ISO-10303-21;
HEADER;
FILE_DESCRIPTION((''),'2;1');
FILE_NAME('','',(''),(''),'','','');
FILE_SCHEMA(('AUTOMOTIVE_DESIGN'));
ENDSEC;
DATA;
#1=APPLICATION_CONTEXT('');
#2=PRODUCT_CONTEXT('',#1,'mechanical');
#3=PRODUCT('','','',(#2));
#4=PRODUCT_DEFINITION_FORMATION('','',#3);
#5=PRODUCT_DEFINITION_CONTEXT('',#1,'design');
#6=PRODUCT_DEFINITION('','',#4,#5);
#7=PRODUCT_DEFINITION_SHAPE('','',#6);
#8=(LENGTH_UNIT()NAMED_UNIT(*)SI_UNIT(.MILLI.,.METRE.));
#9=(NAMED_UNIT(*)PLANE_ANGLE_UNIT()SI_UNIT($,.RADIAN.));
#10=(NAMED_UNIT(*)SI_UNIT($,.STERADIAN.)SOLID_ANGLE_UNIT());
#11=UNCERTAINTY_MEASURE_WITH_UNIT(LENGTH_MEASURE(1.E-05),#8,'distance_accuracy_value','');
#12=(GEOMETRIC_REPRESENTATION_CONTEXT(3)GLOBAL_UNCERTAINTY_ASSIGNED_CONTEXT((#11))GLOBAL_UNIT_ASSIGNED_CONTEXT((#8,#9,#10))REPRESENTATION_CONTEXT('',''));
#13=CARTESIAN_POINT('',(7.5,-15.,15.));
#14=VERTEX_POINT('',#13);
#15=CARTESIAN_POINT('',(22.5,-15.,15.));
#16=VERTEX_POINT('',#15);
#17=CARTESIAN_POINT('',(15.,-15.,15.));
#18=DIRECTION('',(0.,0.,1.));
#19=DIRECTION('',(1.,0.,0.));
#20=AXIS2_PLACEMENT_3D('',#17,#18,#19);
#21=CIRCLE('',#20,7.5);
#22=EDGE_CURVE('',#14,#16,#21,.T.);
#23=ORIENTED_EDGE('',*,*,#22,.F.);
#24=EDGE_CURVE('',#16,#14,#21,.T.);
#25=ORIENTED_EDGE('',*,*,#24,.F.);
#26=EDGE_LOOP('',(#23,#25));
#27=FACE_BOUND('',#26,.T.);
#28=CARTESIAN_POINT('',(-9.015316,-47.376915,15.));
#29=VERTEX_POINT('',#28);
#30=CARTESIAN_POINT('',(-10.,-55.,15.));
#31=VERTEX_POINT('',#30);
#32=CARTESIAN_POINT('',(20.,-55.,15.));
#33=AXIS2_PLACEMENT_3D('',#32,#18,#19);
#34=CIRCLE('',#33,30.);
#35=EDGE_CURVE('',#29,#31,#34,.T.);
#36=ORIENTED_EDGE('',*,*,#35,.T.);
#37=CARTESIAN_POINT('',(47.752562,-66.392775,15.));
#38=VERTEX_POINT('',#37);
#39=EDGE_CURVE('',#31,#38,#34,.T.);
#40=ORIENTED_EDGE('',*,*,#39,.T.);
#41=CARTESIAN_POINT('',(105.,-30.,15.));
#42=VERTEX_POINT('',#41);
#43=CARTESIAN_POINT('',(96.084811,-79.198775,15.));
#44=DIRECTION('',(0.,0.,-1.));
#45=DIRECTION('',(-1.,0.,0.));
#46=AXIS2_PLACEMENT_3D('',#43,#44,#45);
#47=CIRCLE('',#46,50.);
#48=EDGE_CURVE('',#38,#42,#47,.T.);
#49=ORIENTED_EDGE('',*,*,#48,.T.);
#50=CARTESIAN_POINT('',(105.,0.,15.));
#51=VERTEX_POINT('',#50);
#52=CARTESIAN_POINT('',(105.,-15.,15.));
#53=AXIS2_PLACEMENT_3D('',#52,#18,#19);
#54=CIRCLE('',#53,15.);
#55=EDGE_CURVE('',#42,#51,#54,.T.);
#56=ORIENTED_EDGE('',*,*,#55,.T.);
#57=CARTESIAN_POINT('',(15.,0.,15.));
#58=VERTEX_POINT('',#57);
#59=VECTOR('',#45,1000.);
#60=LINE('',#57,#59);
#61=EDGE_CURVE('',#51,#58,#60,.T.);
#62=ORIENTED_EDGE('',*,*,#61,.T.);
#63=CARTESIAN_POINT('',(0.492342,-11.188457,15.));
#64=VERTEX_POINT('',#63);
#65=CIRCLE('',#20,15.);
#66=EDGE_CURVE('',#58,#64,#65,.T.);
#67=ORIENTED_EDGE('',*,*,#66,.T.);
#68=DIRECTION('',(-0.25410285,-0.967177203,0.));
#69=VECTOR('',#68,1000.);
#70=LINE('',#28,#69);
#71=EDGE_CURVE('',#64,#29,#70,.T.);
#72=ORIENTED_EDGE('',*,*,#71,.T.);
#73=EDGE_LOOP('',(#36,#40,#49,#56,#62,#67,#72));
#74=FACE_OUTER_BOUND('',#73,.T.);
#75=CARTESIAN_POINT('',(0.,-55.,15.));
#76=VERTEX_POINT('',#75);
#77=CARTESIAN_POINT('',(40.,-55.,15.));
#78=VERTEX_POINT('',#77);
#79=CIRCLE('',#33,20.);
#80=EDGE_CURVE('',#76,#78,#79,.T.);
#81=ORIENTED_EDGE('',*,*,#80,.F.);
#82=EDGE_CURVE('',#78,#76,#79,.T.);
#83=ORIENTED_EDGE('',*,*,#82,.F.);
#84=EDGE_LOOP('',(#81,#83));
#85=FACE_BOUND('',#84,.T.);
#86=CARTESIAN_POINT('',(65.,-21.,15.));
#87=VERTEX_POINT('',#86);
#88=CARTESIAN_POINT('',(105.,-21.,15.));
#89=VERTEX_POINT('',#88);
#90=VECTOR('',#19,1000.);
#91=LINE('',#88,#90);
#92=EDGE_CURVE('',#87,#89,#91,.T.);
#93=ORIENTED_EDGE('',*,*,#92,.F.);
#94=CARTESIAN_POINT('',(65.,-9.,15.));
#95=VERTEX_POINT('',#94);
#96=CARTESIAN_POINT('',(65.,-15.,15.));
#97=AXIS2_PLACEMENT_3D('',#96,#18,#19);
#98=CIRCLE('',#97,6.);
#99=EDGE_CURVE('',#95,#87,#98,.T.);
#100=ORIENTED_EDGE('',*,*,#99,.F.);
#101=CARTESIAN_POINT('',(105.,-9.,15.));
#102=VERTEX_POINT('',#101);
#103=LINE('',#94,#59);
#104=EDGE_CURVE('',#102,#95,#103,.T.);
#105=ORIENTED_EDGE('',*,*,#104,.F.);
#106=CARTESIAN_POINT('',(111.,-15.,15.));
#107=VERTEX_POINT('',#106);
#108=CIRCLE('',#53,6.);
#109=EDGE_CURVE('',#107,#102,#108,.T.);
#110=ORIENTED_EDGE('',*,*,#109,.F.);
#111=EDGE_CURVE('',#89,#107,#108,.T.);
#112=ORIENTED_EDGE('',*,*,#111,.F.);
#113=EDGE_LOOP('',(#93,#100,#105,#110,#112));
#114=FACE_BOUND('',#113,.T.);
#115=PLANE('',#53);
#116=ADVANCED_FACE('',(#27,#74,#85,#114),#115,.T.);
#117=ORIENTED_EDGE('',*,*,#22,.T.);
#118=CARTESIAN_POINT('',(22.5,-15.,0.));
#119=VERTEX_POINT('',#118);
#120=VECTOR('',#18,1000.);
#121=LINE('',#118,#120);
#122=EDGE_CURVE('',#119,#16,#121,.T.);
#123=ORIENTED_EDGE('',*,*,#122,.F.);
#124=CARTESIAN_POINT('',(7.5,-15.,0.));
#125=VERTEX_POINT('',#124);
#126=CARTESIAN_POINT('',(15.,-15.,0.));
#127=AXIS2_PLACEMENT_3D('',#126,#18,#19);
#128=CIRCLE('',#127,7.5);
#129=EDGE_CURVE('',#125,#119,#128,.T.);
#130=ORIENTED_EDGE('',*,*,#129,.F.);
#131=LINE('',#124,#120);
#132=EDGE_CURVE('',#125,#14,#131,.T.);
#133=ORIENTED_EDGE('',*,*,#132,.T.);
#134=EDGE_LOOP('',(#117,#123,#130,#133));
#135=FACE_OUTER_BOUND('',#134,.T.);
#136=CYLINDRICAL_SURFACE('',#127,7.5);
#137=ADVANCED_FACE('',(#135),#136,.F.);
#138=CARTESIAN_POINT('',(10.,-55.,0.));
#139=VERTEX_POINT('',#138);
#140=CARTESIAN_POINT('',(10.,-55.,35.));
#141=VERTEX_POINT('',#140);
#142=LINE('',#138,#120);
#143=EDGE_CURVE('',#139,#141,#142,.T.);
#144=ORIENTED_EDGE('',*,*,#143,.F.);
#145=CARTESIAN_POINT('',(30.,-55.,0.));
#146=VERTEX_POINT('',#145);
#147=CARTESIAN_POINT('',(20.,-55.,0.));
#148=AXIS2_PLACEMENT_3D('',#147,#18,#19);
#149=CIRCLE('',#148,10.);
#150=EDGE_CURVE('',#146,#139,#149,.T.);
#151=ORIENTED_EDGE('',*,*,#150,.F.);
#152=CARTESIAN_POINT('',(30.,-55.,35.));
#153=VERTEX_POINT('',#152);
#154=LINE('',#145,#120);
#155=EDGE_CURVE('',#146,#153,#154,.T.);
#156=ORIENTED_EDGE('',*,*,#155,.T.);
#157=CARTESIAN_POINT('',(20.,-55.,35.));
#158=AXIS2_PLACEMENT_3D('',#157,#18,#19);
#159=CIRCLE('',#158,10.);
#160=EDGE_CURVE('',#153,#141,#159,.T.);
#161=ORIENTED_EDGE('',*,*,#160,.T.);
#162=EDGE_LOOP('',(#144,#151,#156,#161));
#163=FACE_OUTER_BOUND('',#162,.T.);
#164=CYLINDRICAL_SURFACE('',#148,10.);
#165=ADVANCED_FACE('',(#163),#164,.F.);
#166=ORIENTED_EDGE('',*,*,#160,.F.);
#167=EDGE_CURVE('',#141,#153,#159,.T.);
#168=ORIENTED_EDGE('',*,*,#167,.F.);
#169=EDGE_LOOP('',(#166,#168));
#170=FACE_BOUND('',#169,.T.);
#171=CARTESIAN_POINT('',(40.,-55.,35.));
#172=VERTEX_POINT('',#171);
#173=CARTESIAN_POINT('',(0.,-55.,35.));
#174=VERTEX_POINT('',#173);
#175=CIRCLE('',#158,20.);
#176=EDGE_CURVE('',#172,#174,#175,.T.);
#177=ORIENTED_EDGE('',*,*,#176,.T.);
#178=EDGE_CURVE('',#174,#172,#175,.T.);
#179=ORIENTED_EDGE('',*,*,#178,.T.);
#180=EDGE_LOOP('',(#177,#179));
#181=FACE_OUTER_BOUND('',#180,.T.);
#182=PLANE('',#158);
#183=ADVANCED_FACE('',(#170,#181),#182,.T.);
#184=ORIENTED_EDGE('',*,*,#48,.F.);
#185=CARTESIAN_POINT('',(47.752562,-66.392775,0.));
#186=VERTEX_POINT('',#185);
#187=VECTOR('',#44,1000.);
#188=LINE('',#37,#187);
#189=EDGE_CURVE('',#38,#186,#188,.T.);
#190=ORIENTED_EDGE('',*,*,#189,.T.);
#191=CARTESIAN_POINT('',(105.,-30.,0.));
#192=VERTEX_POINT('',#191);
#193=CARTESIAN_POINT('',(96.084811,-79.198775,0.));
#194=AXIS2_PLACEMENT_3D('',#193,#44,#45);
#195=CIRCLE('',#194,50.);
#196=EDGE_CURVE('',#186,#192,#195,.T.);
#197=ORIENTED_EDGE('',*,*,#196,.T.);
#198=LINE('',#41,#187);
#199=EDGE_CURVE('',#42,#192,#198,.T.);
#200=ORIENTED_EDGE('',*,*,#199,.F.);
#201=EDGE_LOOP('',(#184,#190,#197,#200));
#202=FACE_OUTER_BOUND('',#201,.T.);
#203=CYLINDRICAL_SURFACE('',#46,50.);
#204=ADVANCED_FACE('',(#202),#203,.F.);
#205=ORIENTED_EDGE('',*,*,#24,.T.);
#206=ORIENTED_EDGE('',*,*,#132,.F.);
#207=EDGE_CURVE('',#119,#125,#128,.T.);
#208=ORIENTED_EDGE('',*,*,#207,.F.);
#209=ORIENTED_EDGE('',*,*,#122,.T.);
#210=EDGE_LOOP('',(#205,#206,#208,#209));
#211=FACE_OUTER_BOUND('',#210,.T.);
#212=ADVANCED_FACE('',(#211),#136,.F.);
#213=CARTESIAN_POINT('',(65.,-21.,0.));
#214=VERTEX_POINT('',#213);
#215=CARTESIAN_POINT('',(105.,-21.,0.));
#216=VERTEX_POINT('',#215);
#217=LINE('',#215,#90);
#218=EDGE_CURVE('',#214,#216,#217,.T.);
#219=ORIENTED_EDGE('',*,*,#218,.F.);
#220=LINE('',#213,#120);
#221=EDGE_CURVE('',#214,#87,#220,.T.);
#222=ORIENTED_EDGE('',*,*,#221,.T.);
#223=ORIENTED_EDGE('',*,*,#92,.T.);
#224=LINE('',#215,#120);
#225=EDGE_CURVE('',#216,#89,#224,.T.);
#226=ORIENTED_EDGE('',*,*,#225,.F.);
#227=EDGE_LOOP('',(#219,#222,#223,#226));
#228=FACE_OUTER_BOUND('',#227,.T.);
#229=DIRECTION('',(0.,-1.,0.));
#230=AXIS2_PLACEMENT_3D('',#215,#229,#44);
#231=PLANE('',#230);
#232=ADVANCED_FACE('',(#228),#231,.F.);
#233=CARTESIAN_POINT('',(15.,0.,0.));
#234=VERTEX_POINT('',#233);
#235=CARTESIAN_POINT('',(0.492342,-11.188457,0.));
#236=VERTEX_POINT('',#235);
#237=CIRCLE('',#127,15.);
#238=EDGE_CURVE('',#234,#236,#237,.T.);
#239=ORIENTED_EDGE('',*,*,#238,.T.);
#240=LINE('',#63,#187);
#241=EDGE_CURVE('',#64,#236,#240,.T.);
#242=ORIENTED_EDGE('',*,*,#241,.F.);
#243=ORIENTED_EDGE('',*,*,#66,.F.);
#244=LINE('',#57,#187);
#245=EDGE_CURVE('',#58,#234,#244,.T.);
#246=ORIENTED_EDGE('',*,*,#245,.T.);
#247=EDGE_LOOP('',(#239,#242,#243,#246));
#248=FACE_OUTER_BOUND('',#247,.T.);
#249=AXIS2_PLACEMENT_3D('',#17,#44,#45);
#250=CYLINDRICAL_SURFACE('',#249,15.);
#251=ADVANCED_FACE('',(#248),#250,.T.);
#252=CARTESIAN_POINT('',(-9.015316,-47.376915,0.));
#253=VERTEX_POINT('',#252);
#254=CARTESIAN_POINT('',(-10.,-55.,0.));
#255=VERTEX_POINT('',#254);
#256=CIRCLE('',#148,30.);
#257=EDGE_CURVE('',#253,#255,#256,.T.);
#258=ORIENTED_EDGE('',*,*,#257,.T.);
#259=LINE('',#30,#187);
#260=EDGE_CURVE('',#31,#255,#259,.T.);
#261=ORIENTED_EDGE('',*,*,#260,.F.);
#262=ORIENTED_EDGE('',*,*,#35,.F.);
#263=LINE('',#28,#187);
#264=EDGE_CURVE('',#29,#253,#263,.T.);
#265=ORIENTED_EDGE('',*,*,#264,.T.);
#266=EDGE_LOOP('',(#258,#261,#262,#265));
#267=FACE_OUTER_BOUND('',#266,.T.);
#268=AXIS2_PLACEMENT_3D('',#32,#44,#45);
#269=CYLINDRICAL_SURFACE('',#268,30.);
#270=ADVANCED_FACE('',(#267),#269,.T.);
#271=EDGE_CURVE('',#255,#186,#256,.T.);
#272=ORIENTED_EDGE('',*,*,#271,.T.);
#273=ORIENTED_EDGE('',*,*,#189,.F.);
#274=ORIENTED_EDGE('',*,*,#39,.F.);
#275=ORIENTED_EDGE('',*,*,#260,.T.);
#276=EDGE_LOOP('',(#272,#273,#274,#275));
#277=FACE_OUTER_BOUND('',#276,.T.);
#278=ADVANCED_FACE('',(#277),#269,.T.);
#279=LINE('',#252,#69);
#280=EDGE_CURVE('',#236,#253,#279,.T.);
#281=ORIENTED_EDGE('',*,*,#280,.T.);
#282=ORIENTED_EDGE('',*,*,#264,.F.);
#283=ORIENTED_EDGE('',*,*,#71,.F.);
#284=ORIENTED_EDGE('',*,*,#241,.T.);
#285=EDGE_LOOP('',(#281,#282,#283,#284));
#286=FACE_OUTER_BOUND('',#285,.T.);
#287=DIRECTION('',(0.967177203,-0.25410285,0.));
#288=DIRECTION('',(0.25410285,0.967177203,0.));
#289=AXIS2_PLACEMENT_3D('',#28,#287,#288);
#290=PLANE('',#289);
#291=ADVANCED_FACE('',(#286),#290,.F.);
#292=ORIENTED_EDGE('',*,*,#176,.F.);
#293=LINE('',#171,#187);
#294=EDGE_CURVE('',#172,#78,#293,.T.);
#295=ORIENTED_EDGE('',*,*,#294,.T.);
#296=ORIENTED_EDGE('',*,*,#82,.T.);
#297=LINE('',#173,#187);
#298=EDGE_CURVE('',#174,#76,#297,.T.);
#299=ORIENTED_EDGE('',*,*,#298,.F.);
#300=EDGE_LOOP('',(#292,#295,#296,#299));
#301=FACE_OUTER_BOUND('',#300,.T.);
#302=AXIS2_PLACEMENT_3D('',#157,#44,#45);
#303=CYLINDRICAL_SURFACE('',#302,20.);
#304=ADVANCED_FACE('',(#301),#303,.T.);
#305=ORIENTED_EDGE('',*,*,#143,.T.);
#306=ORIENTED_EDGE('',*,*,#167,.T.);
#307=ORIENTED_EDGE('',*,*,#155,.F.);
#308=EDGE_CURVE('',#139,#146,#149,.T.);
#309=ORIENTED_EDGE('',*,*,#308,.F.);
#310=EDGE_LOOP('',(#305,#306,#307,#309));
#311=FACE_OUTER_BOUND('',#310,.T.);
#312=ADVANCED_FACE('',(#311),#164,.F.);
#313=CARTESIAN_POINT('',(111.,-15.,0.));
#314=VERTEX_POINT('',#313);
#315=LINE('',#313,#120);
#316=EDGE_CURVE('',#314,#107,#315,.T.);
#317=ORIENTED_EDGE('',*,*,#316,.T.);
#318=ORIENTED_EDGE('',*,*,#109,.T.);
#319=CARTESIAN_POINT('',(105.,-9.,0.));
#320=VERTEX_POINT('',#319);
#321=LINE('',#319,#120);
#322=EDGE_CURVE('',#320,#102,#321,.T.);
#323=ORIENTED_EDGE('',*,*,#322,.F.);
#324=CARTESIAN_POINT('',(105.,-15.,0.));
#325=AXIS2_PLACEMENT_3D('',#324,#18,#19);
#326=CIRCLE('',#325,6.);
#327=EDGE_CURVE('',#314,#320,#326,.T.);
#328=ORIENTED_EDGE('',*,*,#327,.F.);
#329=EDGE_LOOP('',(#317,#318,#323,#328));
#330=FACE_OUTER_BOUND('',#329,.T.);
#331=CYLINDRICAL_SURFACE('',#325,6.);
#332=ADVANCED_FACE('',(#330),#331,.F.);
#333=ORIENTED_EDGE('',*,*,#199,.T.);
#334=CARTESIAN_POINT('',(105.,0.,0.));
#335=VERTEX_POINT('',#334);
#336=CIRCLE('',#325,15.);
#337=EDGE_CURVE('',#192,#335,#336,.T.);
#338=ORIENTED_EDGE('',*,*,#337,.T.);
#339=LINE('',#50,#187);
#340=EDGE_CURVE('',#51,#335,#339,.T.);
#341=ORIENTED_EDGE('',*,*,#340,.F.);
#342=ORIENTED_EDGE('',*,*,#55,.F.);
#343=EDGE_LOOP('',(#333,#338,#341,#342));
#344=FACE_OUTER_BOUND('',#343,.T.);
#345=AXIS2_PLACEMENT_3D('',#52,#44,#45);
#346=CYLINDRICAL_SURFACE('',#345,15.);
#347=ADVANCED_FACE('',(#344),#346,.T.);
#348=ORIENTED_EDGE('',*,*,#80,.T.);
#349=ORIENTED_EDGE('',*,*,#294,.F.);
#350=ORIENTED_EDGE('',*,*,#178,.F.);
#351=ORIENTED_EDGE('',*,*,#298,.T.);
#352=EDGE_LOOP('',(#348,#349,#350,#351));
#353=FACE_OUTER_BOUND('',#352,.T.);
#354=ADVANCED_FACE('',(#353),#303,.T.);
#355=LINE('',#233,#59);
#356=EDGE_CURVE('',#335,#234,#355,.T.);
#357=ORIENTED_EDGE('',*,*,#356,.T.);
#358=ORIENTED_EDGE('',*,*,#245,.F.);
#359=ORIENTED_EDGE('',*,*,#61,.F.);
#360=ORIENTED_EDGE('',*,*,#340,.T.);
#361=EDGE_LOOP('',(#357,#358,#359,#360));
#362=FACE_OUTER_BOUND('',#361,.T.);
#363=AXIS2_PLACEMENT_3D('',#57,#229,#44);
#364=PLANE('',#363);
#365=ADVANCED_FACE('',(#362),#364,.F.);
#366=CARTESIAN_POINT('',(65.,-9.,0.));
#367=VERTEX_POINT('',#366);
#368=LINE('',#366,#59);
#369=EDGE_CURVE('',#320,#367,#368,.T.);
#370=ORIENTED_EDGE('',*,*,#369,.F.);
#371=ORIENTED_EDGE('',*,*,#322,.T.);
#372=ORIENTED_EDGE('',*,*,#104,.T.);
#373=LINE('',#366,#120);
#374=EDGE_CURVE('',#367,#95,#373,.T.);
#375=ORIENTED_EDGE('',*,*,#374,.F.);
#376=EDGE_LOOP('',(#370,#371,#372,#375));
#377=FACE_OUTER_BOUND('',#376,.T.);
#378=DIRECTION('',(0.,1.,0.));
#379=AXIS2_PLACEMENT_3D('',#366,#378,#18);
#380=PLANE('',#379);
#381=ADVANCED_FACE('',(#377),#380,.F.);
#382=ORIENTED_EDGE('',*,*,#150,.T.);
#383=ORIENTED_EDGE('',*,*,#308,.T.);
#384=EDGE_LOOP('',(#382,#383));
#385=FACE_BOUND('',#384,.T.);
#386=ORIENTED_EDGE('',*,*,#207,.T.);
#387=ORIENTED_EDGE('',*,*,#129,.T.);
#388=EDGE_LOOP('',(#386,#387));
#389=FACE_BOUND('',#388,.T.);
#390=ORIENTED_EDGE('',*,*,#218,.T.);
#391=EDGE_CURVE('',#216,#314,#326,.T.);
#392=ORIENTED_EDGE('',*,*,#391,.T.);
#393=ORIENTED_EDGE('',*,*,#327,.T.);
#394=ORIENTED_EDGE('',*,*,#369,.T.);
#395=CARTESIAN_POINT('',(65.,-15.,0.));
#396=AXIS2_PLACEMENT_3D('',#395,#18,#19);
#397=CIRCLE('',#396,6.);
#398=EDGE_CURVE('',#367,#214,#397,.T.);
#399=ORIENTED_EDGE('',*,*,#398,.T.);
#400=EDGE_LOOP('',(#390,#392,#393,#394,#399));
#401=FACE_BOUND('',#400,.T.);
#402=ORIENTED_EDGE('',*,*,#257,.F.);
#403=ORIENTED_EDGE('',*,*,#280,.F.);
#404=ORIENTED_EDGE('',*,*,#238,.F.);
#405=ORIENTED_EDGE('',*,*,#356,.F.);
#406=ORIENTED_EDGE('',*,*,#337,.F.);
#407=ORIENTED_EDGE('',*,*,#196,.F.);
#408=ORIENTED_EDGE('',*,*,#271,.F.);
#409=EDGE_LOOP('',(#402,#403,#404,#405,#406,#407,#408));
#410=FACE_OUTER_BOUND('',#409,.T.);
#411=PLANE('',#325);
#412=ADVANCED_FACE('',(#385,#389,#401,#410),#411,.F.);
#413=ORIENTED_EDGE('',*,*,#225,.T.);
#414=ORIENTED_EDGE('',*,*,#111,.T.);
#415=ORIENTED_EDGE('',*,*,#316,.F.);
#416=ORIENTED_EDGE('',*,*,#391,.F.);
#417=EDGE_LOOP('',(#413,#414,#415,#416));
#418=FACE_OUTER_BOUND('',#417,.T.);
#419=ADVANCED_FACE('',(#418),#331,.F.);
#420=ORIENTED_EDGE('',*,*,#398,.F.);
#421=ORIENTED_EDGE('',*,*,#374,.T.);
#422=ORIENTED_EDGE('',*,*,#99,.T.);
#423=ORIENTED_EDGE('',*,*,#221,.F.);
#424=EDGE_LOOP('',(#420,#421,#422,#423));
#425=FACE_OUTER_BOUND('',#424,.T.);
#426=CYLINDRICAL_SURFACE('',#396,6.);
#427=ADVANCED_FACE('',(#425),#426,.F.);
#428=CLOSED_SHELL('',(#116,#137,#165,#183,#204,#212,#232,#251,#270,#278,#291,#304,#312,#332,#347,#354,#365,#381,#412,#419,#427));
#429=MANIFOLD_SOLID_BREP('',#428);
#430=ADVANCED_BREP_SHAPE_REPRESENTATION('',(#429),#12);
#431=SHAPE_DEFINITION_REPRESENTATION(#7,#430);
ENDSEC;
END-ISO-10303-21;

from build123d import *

# Parameters (mm, degrees)
LEVER_PLATE_DEPTH  = 15
HUB_PROFILE_R      = 20
HUB_40_DEPTH       = 20
HUB_BORE_PROFILE_R = 10
HUB_BORE_20_DEPTH  = 35
HOLE_PROFILE_R     = 7.5
HOLE_15_DEPTH      = 15
SLOT_12MM_DEPTH    = 15


with BuildPart() as part:
    # Lever Plate Profile → Lever Plate (new body)
    with BuildSketch(Plane.XY):
        with BuildLine():
            Line((15, 0), (105, 0))
            ThreePointArc((105, 0), (120, -15), (105, -30))
            ThreePointArc((105, -30), (69.260667374, -37.003214388), (47.752561519, -66.392775304))
            ThreePointArc((47.752561519, -66.392775304), (10.471129254, -83.44645184), (-9.015316087, -47.376914511))
            Line((-9.015316087, -47.376914511), (0.492341957, -11.188457255))
            ThreePointArc((0.492341957, -11.188457255), (5.83957264, -3.122013193), (15, 0))
        make_face()
    extrude(amount=LEVER_PLATE_DEPTH)

    # Hub Profile → Hub Ø40 (add)
    with BuildSketch(Plane.XY.offset(15)):
        with Locations((20, -55)):
            Circle(HUB_PROFILE_R)
    extrude(amount=HUB_40_DEPTH)

    # Hub Bore Profile → Hub Bore Ø20 (cut)
    with BuildSketch(Plane.XY.offset(35)):
        with Locations((20, -55)):
            Circle(HUB_BORE_PROFILE_R)
    extrude(amount=-HUB_BORE_20_DEPTH, mode=Mode.SUBTRACT)

    # Hole Profile → Hole Ø15 (cut)
    with BuildSketch(Plane.XY.offset(15)):
        with Locations((15, -15)):
            Circle(HOLE_PROFILE_R)
    extrude(amount=-HOLE_15_DEPTH, mode=Mode.SUBTRACT)

    # Slot Profile → Slot 12mm (cut)
    with BuildSketch(Plane.XY.offset(15)):
        with BuildLine():
            Line((65, -9), (105, -9))
            ThreePointArc((105, -9), (111, -15), (105, -21))
            Line((105, -21), (65, -21))
            ThreePointArc((65, -21), (59, -15), (65, -9))
        make_face()
    extrude(amount=-SLOT_12MM_DEPTH, mode=Mode.SUBTRACT)


solid = part.part
